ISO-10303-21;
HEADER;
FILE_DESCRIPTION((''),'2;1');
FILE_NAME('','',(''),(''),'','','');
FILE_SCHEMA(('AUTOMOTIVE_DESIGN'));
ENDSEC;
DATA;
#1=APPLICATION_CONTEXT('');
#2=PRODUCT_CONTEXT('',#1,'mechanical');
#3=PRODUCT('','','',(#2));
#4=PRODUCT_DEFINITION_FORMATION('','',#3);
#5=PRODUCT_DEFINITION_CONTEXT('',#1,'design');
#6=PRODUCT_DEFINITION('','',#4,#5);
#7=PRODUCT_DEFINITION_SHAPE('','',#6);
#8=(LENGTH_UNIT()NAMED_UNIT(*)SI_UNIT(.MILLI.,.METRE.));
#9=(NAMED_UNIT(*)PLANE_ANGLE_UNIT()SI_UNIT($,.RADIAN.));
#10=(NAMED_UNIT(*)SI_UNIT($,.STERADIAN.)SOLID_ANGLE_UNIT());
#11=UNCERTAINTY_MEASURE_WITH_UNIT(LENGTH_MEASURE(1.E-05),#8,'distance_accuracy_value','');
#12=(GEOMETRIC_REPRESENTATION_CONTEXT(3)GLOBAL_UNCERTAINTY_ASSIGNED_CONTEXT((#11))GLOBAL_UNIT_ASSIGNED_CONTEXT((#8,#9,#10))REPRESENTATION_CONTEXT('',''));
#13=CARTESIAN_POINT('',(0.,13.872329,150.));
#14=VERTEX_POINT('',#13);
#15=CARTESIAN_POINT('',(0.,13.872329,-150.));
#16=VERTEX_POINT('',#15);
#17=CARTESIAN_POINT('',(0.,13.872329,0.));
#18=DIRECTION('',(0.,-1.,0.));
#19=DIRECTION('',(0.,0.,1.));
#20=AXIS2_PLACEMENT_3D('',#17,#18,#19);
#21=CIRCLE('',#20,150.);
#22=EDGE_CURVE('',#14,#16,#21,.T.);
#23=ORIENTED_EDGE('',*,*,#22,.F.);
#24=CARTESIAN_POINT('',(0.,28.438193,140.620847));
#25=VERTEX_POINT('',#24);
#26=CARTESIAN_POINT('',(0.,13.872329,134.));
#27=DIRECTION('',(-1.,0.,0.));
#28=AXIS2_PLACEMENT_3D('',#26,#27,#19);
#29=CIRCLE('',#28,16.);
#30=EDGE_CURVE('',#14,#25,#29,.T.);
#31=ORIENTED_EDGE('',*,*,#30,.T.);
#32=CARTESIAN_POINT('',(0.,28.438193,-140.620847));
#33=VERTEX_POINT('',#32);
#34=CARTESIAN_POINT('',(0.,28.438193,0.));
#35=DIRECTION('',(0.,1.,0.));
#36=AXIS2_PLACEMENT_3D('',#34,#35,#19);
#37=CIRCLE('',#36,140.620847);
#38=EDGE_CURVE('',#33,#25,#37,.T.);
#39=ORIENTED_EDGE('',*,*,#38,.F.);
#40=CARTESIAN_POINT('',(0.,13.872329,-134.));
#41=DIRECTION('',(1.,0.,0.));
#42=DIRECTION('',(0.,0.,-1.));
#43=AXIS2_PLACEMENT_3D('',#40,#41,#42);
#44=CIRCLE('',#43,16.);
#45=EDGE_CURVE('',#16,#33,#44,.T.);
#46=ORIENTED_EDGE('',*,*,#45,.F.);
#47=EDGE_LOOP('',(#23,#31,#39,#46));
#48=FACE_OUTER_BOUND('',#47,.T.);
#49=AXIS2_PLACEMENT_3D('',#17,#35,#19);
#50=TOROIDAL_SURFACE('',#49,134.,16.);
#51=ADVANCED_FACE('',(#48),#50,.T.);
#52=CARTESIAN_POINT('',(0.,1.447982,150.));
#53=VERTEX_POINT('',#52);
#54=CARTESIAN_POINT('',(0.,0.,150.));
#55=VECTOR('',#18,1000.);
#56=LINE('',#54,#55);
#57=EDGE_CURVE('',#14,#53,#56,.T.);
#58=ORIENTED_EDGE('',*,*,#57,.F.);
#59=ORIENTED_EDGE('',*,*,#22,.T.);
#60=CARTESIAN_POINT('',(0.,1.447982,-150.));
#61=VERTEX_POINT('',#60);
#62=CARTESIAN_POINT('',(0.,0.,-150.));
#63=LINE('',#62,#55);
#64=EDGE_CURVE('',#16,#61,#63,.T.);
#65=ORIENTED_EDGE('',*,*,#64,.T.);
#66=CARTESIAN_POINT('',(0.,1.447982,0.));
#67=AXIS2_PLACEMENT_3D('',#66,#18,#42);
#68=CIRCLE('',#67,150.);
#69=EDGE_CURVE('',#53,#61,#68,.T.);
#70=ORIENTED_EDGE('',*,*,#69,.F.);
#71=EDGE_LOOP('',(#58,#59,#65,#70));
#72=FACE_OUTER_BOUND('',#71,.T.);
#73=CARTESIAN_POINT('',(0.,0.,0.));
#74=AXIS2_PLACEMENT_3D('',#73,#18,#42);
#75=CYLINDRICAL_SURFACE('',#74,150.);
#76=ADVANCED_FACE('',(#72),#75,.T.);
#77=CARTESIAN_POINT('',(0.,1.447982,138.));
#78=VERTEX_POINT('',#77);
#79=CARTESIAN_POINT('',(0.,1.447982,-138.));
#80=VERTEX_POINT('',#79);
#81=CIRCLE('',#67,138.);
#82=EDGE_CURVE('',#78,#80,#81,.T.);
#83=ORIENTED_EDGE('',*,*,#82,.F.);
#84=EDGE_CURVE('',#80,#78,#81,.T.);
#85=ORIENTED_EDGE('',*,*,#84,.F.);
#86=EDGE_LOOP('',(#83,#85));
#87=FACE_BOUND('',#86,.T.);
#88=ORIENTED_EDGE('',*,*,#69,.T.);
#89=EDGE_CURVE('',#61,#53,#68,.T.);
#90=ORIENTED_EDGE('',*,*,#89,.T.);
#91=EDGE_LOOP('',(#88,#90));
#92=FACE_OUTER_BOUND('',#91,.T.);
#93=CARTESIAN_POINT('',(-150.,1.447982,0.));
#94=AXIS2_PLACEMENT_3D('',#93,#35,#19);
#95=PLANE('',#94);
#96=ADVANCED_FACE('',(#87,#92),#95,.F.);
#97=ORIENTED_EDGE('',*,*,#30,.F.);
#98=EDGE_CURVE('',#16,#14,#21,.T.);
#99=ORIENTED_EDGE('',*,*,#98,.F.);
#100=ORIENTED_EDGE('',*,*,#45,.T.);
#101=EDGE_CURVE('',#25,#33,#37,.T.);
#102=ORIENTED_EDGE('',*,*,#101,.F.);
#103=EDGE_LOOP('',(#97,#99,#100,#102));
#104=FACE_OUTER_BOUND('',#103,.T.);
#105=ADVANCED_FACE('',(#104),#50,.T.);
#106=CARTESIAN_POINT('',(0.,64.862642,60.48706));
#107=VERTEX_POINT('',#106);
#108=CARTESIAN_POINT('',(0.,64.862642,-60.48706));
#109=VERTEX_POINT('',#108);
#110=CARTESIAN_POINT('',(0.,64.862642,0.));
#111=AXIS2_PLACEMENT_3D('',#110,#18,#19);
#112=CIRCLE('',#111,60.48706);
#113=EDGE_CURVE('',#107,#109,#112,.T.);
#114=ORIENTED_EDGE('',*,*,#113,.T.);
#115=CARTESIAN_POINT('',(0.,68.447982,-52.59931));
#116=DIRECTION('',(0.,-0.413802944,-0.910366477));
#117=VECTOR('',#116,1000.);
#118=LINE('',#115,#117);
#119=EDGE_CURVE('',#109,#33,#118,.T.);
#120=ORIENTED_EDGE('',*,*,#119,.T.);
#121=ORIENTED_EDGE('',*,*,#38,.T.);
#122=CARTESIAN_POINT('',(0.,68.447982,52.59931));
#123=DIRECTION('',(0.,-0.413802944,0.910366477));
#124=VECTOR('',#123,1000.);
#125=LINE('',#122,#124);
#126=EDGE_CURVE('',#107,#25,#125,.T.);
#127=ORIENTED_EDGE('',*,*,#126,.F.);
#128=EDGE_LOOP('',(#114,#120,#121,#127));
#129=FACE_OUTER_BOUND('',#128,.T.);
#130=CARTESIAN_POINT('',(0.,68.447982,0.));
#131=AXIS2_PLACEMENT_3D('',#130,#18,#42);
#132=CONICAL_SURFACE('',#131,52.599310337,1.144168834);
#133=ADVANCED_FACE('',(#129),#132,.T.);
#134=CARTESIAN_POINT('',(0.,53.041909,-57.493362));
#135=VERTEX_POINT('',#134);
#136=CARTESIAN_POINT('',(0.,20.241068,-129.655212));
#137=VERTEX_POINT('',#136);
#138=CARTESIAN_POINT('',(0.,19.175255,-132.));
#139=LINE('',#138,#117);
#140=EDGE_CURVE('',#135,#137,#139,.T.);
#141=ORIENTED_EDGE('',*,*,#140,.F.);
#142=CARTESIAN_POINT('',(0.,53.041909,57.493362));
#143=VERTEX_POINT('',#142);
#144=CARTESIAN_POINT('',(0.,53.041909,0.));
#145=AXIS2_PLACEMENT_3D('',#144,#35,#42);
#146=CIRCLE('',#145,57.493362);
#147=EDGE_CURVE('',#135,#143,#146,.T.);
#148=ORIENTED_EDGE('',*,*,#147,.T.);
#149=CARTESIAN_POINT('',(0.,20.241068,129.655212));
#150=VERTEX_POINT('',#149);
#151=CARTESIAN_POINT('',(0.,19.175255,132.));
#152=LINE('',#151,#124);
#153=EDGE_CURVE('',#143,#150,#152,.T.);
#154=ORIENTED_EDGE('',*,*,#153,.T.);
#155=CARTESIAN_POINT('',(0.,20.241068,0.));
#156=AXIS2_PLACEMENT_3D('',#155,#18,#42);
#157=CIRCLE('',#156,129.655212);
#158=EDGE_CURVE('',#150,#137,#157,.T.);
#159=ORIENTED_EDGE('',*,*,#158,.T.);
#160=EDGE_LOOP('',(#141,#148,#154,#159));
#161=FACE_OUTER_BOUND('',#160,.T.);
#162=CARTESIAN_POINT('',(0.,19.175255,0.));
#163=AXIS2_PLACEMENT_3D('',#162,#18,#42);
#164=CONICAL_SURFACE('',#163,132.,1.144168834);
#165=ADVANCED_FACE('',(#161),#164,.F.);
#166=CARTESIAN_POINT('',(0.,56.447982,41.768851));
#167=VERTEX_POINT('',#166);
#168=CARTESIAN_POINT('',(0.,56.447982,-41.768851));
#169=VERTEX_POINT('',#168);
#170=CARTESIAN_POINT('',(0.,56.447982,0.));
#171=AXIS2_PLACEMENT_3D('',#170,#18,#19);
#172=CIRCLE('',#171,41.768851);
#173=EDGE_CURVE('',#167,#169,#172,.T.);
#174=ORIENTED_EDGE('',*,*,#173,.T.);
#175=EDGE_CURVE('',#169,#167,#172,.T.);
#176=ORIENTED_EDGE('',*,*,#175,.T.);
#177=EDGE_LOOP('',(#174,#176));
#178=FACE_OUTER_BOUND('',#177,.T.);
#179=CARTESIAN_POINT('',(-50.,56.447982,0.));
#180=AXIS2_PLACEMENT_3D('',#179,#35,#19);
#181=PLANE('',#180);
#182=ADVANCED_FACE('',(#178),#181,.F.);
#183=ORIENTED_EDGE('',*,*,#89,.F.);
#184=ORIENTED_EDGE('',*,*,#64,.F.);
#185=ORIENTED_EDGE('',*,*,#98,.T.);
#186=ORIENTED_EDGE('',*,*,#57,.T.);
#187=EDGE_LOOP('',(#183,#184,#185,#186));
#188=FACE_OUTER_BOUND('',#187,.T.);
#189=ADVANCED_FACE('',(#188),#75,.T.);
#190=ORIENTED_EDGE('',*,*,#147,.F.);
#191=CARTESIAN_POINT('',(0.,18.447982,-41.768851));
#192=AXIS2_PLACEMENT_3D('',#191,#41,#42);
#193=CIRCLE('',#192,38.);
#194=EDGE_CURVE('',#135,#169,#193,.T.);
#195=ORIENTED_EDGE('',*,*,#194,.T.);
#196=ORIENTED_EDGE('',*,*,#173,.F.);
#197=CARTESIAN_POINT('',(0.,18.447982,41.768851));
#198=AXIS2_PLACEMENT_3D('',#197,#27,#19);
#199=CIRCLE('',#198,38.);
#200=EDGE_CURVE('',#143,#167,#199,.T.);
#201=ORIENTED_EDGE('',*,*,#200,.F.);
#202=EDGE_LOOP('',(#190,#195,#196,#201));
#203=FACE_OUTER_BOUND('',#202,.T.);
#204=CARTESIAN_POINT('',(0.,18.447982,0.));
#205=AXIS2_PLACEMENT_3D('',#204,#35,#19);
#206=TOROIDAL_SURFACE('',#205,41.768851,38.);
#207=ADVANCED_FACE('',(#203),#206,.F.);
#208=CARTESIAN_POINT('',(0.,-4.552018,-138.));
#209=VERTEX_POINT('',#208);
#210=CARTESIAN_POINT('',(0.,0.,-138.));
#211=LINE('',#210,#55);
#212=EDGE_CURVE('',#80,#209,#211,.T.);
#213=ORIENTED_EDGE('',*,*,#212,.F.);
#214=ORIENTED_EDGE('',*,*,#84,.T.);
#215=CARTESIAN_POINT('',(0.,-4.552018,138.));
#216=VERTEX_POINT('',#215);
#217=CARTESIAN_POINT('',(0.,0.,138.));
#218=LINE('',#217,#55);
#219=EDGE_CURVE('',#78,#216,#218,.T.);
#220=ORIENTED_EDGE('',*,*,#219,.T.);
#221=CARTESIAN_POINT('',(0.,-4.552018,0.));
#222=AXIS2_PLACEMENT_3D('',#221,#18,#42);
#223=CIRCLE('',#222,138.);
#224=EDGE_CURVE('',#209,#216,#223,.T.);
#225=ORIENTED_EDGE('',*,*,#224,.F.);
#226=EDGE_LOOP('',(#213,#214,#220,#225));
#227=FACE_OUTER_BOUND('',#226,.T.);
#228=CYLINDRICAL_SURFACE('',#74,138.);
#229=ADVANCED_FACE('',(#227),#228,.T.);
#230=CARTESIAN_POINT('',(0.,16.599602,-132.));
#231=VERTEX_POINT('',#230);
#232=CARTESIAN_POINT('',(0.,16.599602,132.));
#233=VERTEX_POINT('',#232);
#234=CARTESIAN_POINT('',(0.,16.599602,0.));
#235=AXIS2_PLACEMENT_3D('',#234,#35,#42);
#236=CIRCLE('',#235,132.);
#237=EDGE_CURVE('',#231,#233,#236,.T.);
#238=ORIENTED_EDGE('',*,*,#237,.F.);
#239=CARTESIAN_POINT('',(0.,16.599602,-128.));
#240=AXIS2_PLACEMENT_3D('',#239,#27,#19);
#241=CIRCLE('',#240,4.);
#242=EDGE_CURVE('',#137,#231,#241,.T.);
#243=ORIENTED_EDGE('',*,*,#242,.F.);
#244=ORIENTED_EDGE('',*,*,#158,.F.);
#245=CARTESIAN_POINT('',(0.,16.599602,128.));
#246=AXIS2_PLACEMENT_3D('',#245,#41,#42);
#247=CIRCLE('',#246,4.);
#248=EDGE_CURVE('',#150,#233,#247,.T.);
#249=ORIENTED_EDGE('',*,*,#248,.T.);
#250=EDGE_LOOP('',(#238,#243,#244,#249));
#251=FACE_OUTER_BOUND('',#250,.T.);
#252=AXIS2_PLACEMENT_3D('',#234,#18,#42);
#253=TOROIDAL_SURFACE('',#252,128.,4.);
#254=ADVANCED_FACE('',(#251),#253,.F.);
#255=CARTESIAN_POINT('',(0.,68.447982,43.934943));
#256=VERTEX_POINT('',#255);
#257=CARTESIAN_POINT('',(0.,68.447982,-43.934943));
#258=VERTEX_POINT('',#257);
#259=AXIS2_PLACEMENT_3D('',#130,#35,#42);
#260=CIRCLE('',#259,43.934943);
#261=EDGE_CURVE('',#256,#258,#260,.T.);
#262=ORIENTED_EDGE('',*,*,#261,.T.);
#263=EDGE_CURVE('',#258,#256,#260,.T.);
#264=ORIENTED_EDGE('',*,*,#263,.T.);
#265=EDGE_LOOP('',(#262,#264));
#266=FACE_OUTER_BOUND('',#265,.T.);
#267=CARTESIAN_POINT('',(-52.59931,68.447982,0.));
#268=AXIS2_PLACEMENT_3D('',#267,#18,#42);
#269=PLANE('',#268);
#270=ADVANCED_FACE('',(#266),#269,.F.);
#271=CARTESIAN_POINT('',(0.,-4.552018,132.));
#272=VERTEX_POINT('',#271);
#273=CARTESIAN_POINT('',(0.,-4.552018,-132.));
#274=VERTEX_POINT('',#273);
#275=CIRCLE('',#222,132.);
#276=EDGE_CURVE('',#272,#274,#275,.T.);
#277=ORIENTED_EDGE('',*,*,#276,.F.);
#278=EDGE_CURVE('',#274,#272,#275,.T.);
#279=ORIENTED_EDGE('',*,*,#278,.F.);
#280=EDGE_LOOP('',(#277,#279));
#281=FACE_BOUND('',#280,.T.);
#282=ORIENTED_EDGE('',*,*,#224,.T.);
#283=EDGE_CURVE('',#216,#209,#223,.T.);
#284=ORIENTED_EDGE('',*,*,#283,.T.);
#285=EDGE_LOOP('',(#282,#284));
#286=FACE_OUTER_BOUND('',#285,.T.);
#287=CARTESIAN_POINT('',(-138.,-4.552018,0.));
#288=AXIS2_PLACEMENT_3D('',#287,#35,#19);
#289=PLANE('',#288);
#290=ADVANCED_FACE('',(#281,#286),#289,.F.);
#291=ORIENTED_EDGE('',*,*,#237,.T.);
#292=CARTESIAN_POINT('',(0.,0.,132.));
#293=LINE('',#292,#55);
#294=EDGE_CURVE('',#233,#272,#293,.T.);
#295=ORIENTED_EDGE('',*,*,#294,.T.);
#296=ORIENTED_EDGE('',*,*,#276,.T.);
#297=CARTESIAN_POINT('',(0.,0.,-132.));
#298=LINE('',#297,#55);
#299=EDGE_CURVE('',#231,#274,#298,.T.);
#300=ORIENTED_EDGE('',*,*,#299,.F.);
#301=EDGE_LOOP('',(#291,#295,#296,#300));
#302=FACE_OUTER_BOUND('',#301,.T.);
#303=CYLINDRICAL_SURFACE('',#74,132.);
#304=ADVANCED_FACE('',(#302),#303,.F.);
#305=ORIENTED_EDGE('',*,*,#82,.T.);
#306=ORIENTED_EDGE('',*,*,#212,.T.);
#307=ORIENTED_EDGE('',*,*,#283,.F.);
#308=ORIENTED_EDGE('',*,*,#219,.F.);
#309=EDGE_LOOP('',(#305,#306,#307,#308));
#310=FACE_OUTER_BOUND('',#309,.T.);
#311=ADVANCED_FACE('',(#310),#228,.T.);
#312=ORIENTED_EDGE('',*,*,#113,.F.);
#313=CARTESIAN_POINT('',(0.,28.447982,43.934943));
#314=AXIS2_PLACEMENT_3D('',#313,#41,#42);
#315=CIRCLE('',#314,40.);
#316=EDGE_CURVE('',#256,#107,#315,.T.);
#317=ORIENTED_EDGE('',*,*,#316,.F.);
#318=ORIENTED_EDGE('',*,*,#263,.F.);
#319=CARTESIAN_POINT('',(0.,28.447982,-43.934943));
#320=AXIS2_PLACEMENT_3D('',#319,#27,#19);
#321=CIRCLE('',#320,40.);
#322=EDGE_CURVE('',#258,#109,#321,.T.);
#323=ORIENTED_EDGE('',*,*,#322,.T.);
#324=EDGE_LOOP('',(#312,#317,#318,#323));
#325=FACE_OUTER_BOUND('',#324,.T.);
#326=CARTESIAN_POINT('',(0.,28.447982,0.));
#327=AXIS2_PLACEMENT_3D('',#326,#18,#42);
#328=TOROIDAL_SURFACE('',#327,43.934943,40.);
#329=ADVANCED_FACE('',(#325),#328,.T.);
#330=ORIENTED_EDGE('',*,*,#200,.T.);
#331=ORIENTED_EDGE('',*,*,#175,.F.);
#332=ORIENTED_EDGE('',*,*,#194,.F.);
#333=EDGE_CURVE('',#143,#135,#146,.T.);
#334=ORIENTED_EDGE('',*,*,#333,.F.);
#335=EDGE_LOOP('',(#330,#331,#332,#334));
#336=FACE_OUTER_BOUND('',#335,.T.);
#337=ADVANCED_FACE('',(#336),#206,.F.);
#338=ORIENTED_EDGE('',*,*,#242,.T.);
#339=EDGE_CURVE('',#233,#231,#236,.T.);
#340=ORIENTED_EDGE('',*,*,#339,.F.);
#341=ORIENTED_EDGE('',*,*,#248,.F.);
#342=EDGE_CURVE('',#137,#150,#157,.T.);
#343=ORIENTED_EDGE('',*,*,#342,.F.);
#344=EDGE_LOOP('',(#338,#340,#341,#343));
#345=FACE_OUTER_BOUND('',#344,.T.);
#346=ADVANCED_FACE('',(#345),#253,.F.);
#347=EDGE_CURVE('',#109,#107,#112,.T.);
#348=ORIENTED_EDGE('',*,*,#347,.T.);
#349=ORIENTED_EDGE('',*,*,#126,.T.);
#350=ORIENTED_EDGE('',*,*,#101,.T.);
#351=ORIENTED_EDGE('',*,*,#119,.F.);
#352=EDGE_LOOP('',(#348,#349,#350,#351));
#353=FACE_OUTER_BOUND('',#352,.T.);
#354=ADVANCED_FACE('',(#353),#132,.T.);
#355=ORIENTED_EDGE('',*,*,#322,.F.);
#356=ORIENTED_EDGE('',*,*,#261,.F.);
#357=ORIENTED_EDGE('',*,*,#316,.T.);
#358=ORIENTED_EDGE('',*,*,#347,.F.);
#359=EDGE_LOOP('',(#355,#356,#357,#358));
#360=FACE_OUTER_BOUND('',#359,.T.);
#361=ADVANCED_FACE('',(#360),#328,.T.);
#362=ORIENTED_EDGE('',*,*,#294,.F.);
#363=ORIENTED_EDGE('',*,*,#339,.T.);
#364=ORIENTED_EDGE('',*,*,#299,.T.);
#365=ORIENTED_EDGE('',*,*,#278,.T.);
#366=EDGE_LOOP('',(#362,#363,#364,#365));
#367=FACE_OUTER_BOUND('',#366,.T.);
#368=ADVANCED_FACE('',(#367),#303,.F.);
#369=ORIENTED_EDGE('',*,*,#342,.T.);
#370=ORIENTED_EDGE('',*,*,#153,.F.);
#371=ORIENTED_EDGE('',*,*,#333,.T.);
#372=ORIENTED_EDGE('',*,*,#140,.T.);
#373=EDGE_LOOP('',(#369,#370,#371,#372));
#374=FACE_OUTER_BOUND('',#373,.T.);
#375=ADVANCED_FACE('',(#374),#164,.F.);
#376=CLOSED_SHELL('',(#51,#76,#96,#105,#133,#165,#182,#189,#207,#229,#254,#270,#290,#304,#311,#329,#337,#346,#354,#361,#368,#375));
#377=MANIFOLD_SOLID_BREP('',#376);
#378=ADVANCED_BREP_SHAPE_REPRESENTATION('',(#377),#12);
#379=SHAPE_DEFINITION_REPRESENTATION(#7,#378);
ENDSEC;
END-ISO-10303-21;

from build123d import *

# Parameters (mm, degrees)
FILLET1_R = 40
FILLET2_R = 38
FILLET3_R = 16
FILLET4_R = 4


with BuildPart() as part:
    # Sketch1 → Revolve1 (revolve)
    with BuildSketch(Plane.XY, mode=Mode.PRIVATE) as revolve1_sk:
        Polygon((-150, 1.447982474), (-150, 24.174941718), (-52.599310337, 68.447982474), (0, 68.447982474), (0, 56.447982474), (-50, 56.447982474), (-132, 19.175255201), (-132, 1.447982474), (-132, -4.552017526), (-138, -4.552017526), (-138, 1.447982474), align=None)
    revolve(revolve1_sk.sketch.rotate(Axis((0, 0, 0), (0, 1, 0)), 270), axis=Axis((0, 0, 0), (0, 1, 0)))

    # Fillet1
    fillet1_edges = [part.edges().sort_by_distance(p)[0] for p in [
        (0, 68.447982474, 52.599310337),
    ]]
    fillet(fillet1_edges, radius=FILLET1_R)

    # Fillet2
    fillet2_edges = [part.edges().sort_by_distance(p)[0] for p in [
        (0, 56.447982474, 50),
    ]]
    fillet(fillet2_edges, radius=FILLET2_R)

    # Fillet3
    fillet3_edges = [part.edges().sort_by_distance(p)[0] for p in [
        (0, 24.174941718, 150),
    ]]
    fillet(fillet3_edges, radius=FILLET3_R)

    # Fillet4
    fillet4_edges = [part.edges().sort_by_distance(p)[0] for p in [
        (0, 19.175255201, 132),
    ]]
    fillet(fillet4_edges, radius=FILLET4_R)


solid = part.part
